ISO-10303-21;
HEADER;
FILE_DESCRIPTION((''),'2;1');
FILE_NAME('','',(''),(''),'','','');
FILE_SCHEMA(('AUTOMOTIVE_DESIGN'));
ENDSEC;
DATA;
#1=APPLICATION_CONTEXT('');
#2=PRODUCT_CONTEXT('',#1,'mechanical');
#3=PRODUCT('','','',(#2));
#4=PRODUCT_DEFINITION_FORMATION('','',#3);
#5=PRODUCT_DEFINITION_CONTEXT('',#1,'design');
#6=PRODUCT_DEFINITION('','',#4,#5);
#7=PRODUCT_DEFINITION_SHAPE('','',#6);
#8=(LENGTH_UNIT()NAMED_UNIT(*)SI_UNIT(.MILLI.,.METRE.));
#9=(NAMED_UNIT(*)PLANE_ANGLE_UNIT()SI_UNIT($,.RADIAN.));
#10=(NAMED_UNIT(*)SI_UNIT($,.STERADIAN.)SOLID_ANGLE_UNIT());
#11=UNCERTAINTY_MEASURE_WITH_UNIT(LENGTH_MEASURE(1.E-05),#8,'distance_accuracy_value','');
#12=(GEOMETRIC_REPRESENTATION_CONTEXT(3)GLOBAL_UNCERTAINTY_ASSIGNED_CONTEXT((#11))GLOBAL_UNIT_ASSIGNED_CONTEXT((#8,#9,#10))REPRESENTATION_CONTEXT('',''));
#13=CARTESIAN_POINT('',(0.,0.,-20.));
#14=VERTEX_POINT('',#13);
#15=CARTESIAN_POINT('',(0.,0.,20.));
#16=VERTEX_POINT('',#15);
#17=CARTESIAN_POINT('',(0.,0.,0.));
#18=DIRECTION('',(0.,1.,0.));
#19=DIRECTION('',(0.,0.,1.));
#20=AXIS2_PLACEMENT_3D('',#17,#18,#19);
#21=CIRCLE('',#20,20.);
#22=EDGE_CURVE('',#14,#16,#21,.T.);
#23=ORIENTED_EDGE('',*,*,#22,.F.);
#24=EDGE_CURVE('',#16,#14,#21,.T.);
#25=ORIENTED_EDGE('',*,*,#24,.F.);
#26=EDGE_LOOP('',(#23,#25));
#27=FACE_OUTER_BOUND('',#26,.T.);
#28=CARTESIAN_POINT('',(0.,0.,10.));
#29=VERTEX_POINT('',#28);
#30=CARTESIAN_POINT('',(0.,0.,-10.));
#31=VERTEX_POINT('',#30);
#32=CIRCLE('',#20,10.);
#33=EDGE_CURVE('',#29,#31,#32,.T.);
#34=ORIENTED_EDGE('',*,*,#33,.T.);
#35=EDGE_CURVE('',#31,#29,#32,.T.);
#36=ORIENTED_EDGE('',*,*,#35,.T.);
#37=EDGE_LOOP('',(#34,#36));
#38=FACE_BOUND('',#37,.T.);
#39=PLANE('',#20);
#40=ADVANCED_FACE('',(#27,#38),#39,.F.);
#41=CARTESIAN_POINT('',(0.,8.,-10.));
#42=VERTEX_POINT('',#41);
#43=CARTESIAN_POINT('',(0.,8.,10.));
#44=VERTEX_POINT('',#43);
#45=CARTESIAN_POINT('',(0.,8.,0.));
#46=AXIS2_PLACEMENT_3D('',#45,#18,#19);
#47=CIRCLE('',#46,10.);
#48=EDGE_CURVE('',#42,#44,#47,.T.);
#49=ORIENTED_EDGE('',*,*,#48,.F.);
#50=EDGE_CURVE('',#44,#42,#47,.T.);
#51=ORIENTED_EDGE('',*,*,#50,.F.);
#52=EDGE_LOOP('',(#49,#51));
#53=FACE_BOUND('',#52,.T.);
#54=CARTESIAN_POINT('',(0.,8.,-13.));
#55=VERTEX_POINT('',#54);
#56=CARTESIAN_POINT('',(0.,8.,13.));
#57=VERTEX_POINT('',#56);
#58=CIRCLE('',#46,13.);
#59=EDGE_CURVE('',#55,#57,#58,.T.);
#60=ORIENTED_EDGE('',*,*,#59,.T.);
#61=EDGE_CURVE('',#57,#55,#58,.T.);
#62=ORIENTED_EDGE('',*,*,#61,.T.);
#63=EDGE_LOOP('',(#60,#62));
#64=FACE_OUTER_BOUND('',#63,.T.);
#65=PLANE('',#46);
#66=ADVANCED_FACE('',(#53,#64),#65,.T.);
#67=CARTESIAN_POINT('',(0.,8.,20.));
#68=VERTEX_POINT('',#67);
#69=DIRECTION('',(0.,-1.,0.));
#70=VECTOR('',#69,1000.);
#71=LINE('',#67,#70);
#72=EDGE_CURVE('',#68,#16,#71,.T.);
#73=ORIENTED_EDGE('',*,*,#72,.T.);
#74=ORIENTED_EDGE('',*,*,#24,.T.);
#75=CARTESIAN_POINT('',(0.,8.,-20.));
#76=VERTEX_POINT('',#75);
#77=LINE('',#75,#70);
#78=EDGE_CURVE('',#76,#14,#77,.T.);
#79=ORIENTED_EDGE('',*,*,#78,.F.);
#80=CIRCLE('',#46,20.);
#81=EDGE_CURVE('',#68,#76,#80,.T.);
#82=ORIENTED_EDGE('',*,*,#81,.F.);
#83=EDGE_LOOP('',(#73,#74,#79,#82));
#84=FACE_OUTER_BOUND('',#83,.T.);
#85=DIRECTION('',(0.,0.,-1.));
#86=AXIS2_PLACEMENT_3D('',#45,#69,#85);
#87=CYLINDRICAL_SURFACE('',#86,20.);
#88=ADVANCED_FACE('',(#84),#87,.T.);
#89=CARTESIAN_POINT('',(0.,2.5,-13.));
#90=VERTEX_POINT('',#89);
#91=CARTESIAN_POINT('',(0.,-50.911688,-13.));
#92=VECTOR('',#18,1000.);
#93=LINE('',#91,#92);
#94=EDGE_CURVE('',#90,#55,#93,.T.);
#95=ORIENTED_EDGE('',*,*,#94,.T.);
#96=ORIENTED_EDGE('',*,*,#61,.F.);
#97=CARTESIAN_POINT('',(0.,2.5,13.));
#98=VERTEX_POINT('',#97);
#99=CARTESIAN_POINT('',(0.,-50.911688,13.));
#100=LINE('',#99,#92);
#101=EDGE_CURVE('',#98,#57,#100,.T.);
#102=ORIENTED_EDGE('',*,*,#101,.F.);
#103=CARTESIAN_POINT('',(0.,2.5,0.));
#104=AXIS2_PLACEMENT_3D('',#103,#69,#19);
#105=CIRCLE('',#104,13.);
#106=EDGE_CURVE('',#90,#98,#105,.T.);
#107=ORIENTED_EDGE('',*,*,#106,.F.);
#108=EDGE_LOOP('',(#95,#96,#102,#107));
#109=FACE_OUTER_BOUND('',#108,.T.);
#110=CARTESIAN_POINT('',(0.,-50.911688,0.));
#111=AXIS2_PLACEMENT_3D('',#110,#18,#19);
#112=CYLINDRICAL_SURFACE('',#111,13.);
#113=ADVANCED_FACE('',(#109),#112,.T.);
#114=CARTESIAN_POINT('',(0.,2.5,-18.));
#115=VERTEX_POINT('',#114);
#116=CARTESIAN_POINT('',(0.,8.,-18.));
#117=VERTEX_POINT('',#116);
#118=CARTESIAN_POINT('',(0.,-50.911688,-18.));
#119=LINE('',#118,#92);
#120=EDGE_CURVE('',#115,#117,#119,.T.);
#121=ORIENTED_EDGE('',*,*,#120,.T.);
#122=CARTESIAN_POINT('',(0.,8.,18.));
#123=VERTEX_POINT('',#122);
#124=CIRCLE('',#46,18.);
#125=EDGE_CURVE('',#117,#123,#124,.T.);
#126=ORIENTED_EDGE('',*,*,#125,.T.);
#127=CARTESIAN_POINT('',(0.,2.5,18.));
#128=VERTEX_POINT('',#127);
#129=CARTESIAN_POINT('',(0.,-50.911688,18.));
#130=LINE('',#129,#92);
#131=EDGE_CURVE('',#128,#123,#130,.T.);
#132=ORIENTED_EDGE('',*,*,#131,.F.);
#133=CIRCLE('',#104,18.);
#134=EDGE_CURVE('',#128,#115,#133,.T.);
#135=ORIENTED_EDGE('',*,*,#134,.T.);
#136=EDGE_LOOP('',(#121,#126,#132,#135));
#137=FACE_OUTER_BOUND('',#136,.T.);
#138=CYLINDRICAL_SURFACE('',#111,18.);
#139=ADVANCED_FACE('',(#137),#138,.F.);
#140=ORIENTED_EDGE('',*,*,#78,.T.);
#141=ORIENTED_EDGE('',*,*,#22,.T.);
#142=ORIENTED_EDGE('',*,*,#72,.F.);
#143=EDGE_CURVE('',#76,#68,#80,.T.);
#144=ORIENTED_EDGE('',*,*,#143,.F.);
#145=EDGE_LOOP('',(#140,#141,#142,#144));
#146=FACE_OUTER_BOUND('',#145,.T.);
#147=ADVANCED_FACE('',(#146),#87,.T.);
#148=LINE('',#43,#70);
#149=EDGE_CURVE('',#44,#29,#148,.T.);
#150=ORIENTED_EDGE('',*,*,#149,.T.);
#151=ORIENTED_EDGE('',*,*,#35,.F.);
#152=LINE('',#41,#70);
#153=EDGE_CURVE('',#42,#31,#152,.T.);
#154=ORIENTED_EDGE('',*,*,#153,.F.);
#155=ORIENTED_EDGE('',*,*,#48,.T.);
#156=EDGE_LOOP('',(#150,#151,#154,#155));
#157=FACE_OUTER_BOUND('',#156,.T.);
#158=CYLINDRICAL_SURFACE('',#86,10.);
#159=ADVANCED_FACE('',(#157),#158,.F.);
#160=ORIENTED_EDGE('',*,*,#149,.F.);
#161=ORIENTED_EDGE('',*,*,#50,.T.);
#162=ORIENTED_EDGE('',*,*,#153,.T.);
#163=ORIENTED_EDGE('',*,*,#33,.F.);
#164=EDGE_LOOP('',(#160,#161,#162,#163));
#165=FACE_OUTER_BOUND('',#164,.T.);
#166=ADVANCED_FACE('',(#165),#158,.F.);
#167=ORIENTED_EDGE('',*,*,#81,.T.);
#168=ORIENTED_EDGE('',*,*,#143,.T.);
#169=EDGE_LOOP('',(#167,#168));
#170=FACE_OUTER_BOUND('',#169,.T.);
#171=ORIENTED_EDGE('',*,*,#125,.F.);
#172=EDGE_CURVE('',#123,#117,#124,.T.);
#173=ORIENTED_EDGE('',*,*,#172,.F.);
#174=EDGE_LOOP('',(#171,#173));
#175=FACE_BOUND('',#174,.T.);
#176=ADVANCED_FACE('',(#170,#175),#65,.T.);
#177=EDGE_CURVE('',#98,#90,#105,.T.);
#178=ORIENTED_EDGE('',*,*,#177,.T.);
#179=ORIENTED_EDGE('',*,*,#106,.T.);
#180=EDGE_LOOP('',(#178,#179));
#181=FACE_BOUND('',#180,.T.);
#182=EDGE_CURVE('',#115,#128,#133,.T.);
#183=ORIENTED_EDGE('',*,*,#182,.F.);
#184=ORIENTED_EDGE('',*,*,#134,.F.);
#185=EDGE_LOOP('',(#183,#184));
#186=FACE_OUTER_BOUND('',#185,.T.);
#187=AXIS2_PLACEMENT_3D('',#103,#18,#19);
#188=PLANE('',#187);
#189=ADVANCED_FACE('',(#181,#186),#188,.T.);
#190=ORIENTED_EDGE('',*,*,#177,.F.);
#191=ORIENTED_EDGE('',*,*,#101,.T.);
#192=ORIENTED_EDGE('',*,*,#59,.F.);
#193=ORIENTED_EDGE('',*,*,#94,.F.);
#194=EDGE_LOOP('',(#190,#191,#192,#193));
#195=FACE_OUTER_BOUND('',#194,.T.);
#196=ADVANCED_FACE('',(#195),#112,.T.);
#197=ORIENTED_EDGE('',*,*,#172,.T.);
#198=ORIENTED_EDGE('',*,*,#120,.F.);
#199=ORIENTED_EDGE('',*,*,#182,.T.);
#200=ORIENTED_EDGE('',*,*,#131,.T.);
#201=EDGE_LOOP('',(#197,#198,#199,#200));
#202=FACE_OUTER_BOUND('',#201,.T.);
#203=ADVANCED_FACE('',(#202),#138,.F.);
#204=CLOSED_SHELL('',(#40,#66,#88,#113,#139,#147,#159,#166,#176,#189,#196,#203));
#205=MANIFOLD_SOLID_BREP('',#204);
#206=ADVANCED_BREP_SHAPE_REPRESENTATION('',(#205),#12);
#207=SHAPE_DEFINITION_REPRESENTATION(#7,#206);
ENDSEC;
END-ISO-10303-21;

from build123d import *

# Parameters (mm, degrees)
SKETCH1_R           = 20
SKETCH1_R_2         = 10
BOSS_EXTRUDE1_DEPTH = 8
SKETCH2_R           = 18
SKETCH2_R_2         = 13
CUT_EXTRUDE1_DEPTH  = 5.5


with BuildPart() as part:
    # Sketch1 → Boss-Extrude1 (new body)
    with BuildSketch(Plane(origin=(0, 0, 0), x_dir=(1, 0, 0), z_dir=(0, 1, 0))):
        with Locations(Location((0, 0, 0), (0, 0, 270))):
            Circle(SKETCH1_R)
        with Locations(Location((0, 0, 0), (0, 0, 270))):
            Circle(SKETCH1_R_2, mode=Mode.SUBTRACT)
    extrude(amount=BOSS_EXTRUDE1_DEPTH)

    # Sketch2 → Cut-Extrude1 (cut)
    with BuildSketch(Plane(origin=(0, 8, 0), x_dir=(1, 0, 0), z_dir=(0, 1, 0))):
        with Locations(Location((0, 0, 0), (0, 0, 270))):
            Circle(SKETCH2_R)
        with Locations(Location((0, 0, 0), (0, 0, 270))):
            Circle(SKETCH2_R_2, mode=Mode.SUBTRACT)
    extrude(amount=-CUT_EXTRUDE1_DEPTH, mode=Mode.SUBTRACT)


solid = part.part
